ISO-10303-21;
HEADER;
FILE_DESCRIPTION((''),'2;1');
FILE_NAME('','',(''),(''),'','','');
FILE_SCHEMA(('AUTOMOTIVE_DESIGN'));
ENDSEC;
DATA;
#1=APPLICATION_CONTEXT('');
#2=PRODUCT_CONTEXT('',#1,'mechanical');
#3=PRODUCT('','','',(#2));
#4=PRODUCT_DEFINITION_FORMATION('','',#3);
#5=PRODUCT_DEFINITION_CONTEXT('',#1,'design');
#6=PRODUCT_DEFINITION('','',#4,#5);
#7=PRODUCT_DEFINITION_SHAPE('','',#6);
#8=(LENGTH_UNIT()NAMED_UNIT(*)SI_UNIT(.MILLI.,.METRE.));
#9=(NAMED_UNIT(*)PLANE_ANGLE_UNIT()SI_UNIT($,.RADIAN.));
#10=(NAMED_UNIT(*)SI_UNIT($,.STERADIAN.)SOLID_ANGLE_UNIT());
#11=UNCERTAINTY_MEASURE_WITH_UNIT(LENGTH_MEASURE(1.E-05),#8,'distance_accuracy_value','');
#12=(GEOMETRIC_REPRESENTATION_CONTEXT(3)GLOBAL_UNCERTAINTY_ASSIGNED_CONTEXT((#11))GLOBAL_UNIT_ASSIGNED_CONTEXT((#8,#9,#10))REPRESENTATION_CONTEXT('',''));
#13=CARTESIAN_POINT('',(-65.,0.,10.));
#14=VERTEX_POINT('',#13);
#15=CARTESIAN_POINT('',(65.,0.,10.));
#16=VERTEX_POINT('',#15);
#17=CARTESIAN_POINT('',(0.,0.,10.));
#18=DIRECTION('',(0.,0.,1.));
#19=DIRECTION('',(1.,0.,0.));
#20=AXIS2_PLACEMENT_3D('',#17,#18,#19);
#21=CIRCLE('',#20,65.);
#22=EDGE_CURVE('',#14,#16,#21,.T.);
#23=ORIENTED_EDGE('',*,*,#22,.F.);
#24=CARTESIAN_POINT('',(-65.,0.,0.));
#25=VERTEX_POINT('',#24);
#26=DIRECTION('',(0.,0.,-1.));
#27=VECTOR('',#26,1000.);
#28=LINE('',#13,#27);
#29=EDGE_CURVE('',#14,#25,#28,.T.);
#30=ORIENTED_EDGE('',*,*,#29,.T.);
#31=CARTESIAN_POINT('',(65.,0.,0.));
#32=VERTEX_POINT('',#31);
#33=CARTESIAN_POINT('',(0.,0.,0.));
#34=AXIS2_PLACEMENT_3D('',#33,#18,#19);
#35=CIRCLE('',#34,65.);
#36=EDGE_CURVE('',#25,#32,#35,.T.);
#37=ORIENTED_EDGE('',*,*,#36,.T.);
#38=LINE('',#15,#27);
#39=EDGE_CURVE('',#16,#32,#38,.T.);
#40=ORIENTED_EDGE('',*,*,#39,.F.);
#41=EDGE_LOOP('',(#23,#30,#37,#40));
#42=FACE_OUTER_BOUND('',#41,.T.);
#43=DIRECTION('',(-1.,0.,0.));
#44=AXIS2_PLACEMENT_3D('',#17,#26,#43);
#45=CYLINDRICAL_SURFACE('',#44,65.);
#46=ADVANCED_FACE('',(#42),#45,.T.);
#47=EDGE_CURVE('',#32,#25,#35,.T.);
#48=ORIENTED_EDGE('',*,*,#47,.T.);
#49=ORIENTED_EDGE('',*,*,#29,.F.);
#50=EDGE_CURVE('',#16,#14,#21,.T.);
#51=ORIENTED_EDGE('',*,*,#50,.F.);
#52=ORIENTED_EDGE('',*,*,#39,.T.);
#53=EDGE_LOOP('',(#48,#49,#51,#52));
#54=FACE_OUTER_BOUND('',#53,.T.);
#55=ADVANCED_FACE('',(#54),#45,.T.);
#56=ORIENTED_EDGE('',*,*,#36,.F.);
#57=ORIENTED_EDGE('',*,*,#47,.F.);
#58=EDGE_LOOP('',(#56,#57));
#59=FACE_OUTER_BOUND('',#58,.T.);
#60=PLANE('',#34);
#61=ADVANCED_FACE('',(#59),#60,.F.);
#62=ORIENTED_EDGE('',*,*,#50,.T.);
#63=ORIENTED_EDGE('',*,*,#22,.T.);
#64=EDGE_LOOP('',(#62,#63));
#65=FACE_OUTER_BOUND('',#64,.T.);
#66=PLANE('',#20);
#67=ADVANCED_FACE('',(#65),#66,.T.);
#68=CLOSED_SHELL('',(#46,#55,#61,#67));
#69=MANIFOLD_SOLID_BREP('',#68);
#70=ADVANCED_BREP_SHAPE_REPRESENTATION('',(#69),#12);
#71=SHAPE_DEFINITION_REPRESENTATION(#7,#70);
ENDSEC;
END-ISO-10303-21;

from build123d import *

# Parameters (mm, degrees)
SKETCH1_R           = 65
BOSS_EXTRUDE1_DEPTH = 10


with BuildPart() as part:
    # Sketch1 → Boss-Extrude1 (new body)
    with BuildSketch(Plane.XY):
        Circle(SKETCH1_R)
    extrude(amount=BOSS_EXTRUDE1_DEPTH)


solid = part.part
